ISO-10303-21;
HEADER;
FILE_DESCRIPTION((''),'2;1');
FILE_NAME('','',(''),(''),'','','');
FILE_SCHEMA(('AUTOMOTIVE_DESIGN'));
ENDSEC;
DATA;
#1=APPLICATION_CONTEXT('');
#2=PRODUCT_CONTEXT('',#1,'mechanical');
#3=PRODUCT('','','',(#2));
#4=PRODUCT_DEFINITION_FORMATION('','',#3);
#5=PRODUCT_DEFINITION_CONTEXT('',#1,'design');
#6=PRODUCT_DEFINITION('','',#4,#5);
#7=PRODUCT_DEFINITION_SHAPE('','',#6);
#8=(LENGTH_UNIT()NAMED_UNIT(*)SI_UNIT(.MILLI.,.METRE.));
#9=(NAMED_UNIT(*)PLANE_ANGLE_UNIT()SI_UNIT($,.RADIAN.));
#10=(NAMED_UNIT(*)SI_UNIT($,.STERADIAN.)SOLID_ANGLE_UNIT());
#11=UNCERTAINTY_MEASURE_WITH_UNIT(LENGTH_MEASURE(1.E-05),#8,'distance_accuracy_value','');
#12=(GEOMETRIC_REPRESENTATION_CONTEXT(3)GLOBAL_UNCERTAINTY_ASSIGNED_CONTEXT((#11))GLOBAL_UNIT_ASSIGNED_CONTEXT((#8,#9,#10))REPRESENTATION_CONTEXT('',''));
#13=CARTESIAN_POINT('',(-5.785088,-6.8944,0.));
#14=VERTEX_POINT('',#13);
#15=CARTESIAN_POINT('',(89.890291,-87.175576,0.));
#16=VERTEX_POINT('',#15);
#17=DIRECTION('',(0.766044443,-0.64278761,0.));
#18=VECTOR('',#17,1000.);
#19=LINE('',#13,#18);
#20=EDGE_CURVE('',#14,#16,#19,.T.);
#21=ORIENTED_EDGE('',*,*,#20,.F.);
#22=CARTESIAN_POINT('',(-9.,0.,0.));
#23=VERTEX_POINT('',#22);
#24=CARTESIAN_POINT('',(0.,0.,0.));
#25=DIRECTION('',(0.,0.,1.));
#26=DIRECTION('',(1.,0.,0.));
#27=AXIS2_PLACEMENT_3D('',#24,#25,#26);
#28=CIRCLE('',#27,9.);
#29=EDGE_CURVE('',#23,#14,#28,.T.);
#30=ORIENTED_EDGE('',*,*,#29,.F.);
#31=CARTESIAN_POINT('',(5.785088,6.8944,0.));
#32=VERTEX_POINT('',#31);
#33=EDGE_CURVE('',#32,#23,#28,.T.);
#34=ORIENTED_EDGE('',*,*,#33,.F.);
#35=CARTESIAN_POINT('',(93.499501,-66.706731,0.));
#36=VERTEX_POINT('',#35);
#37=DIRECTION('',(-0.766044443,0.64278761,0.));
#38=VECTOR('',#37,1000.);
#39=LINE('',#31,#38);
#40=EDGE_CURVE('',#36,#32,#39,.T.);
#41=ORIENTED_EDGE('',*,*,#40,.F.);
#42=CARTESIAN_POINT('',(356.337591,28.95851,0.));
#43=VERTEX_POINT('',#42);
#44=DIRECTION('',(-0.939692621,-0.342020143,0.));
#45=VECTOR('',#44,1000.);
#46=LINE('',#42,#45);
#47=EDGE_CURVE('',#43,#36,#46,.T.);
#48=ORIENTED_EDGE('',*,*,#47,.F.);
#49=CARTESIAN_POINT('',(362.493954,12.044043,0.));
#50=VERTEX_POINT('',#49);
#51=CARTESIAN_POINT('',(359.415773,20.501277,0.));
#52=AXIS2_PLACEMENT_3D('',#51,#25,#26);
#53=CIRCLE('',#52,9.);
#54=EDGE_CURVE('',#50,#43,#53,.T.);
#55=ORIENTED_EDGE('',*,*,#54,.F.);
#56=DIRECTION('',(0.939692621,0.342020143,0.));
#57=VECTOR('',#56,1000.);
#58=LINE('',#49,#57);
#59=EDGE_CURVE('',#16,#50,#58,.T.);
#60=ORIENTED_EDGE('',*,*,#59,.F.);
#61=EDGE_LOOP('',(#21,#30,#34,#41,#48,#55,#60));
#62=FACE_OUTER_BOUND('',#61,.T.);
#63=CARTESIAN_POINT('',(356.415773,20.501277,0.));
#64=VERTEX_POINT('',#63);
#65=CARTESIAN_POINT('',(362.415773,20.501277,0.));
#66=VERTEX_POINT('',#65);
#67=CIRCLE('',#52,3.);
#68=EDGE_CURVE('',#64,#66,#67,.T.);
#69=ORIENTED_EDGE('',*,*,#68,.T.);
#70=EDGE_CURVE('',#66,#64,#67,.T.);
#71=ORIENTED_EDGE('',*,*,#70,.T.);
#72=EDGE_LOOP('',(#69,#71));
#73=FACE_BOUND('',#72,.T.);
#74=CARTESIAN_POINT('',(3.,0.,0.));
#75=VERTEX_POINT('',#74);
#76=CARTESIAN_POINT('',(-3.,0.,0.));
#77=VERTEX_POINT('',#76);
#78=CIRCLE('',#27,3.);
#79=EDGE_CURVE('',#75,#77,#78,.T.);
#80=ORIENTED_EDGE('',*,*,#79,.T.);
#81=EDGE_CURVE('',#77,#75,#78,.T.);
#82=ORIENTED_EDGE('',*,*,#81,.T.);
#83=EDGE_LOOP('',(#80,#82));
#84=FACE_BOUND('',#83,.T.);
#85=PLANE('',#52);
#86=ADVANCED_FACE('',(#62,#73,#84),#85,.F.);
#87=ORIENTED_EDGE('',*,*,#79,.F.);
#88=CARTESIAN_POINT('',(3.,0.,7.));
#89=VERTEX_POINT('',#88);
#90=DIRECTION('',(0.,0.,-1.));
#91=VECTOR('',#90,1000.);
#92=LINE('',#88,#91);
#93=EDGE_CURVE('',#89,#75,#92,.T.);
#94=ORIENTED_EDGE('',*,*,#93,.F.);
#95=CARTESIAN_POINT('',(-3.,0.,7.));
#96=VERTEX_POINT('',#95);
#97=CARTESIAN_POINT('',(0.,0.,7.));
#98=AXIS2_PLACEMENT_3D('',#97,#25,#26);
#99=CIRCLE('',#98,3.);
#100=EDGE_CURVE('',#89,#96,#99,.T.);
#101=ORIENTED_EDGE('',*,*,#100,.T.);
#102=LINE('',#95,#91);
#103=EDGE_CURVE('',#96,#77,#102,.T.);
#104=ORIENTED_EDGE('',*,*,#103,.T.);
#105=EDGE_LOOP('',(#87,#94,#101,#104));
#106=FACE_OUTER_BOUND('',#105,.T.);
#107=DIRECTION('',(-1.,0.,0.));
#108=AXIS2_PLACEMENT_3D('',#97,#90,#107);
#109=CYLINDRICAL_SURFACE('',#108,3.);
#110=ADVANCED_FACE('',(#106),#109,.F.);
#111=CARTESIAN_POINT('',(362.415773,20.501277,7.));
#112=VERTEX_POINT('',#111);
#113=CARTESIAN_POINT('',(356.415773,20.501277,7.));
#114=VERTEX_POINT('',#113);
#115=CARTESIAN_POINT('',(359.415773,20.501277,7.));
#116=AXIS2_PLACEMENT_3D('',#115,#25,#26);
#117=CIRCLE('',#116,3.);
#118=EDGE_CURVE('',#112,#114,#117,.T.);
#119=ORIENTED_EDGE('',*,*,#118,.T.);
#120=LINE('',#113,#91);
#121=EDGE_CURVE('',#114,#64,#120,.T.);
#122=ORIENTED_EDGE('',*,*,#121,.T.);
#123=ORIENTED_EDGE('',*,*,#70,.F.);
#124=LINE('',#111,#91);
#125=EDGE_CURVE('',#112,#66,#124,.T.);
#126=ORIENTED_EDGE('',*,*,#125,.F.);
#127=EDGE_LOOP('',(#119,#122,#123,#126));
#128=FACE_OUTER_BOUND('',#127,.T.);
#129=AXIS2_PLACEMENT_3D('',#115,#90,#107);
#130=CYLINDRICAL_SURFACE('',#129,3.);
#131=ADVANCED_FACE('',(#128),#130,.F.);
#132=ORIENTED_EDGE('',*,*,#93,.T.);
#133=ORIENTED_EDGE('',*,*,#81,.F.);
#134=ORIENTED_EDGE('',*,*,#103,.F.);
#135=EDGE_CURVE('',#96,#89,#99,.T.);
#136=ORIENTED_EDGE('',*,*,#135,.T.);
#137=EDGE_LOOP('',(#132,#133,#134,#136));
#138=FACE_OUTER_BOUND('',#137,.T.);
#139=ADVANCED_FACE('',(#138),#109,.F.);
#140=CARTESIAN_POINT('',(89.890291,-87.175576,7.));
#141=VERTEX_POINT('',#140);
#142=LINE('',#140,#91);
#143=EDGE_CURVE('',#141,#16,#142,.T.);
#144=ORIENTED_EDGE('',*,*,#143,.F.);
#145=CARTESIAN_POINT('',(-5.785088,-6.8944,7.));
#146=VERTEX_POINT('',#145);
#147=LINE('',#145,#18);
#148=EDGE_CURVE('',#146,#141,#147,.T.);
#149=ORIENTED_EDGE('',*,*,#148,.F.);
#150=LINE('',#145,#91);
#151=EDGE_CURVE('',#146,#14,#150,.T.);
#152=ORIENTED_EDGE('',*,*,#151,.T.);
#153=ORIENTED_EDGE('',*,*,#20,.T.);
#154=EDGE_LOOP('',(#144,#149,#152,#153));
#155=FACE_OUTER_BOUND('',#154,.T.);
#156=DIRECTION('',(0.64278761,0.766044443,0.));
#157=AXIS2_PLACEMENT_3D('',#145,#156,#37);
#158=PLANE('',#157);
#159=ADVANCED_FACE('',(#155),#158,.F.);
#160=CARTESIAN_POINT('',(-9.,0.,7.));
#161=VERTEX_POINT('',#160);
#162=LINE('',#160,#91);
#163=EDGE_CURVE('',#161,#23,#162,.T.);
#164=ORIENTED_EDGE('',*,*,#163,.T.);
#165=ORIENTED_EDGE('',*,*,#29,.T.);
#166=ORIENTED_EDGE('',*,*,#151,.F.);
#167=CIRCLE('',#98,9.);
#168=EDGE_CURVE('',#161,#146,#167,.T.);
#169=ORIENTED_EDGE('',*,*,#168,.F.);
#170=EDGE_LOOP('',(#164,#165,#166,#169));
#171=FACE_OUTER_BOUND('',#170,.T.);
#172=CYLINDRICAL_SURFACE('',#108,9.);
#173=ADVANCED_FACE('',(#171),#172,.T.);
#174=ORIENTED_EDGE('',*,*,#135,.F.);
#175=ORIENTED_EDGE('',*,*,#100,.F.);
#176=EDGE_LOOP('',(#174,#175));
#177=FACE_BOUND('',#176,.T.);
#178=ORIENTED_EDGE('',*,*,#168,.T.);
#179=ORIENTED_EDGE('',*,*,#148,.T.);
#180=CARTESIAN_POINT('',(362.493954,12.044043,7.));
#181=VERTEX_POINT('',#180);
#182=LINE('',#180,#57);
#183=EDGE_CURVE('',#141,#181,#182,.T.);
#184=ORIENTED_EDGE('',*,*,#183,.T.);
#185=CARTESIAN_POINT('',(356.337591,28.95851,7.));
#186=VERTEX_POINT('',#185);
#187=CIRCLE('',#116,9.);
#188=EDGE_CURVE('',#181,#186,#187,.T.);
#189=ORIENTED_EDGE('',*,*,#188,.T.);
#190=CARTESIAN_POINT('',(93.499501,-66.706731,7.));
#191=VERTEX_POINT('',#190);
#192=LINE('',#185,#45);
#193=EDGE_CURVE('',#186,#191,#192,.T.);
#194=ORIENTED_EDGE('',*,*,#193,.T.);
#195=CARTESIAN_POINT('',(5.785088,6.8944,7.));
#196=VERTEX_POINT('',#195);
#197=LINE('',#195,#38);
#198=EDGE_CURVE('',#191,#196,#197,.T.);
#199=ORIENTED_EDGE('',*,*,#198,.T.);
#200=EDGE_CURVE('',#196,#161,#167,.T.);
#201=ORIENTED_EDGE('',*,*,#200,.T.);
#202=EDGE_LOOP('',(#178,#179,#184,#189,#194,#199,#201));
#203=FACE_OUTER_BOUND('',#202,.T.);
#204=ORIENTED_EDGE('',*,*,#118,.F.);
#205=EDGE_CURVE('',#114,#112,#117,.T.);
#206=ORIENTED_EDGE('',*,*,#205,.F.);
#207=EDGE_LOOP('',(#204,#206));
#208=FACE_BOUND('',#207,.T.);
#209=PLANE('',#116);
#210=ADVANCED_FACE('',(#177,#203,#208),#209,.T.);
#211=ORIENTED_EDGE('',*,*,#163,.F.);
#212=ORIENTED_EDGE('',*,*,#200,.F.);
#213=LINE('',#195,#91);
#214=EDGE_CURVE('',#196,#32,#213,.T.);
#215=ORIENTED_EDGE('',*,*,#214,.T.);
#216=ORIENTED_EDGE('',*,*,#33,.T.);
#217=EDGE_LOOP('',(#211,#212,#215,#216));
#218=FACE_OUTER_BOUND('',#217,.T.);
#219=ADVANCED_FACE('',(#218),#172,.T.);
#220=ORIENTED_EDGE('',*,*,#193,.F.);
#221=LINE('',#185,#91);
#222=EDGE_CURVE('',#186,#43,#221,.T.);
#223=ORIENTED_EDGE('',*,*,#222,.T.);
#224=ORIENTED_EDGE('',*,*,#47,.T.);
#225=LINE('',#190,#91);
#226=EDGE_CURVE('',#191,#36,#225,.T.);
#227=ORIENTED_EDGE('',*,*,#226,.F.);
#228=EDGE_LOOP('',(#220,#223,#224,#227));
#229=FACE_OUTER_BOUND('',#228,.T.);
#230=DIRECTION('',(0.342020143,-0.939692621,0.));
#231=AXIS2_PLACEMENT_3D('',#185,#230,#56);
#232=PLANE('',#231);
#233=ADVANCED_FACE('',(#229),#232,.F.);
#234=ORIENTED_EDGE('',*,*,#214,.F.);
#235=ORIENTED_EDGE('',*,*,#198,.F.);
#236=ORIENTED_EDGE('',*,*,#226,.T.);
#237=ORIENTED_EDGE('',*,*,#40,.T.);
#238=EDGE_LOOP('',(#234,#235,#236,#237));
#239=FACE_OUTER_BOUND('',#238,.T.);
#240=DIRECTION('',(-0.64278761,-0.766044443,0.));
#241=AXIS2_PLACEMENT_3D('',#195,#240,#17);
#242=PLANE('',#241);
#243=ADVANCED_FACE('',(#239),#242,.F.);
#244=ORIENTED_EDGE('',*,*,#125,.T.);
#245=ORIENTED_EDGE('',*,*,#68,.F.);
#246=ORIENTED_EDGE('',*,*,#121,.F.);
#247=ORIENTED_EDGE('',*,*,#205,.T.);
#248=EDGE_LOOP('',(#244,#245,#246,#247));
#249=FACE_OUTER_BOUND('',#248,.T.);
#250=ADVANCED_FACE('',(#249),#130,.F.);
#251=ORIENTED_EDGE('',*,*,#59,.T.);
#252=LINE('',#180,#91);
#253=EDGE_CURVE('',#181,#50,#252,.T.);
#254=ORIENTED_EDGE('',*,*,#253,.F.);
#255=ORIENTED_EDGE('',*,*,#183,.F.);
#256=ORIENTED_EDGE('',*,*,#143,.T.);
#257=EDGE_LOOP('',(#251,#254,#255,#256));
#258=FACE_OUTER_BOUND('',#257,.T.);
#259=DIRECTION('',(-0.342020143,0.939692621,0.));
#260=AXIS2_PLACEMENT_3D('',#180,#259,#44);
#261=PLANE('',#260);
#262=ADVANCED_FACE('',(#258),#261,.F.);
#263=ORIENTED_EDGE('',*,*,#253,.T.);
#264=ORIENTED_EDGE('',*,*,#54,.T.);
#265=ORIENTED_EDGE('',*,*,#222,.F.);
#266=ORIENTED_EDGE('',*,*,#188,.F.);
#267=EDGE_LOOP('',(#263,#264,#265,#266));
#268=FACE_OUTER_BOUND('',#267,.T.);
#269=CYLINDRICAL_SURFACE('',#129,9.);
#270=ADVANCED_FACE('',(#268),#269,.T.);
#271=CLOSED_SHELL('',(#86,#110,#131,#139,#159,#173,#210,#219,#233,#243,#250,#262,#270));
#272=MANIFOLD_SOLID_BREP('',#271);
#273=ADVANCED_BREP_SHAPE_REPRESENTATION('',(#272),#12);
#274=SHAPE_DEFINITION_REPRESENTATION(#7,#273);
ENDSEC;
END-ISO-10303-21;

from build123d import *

# Parameters (mm, degrees)
SKETCH_1_R      = 3
EXTRUDE_1_DEPTH = 7


with BuildPart() as part:
    # 草图1 → 凸台-拉伸1 (new body)
    with BuildSketch(Plane.XY):
        with BuildLine():
            Line((362.493953978, 12.044043029), (89.890291348, -87.17557592))
            Line((89.890291348, -87.17557592), (-5.785088487, -6.894399988))
            ThreePointArc((-5.785088487, -6.894399988), (-6.894399988, 5.785088487), (5.785088487, 6.894399988))
            Line((5.785088487, 6.894399988), (93.499500944, -66.706731154))
            Line((93.499500944, -66.706731154), (356.337591398, 28.958510203))
            ThreePointArc((356.337591398, 28.958510203), (367.873006275, 23.579457906), (362.493953978, 12.044043029))
        make_face()
        with Locations((359.415772688, 20.501276616)):
            Circle(SKETCH_1_R, mode=Mode.SUBTRACT)
        Circle(SKETCH_1_R, mode=Mode.SUBTRACT)
    extrude(amount=EXTRUDE_1_DEPTH)


solid = part.part
